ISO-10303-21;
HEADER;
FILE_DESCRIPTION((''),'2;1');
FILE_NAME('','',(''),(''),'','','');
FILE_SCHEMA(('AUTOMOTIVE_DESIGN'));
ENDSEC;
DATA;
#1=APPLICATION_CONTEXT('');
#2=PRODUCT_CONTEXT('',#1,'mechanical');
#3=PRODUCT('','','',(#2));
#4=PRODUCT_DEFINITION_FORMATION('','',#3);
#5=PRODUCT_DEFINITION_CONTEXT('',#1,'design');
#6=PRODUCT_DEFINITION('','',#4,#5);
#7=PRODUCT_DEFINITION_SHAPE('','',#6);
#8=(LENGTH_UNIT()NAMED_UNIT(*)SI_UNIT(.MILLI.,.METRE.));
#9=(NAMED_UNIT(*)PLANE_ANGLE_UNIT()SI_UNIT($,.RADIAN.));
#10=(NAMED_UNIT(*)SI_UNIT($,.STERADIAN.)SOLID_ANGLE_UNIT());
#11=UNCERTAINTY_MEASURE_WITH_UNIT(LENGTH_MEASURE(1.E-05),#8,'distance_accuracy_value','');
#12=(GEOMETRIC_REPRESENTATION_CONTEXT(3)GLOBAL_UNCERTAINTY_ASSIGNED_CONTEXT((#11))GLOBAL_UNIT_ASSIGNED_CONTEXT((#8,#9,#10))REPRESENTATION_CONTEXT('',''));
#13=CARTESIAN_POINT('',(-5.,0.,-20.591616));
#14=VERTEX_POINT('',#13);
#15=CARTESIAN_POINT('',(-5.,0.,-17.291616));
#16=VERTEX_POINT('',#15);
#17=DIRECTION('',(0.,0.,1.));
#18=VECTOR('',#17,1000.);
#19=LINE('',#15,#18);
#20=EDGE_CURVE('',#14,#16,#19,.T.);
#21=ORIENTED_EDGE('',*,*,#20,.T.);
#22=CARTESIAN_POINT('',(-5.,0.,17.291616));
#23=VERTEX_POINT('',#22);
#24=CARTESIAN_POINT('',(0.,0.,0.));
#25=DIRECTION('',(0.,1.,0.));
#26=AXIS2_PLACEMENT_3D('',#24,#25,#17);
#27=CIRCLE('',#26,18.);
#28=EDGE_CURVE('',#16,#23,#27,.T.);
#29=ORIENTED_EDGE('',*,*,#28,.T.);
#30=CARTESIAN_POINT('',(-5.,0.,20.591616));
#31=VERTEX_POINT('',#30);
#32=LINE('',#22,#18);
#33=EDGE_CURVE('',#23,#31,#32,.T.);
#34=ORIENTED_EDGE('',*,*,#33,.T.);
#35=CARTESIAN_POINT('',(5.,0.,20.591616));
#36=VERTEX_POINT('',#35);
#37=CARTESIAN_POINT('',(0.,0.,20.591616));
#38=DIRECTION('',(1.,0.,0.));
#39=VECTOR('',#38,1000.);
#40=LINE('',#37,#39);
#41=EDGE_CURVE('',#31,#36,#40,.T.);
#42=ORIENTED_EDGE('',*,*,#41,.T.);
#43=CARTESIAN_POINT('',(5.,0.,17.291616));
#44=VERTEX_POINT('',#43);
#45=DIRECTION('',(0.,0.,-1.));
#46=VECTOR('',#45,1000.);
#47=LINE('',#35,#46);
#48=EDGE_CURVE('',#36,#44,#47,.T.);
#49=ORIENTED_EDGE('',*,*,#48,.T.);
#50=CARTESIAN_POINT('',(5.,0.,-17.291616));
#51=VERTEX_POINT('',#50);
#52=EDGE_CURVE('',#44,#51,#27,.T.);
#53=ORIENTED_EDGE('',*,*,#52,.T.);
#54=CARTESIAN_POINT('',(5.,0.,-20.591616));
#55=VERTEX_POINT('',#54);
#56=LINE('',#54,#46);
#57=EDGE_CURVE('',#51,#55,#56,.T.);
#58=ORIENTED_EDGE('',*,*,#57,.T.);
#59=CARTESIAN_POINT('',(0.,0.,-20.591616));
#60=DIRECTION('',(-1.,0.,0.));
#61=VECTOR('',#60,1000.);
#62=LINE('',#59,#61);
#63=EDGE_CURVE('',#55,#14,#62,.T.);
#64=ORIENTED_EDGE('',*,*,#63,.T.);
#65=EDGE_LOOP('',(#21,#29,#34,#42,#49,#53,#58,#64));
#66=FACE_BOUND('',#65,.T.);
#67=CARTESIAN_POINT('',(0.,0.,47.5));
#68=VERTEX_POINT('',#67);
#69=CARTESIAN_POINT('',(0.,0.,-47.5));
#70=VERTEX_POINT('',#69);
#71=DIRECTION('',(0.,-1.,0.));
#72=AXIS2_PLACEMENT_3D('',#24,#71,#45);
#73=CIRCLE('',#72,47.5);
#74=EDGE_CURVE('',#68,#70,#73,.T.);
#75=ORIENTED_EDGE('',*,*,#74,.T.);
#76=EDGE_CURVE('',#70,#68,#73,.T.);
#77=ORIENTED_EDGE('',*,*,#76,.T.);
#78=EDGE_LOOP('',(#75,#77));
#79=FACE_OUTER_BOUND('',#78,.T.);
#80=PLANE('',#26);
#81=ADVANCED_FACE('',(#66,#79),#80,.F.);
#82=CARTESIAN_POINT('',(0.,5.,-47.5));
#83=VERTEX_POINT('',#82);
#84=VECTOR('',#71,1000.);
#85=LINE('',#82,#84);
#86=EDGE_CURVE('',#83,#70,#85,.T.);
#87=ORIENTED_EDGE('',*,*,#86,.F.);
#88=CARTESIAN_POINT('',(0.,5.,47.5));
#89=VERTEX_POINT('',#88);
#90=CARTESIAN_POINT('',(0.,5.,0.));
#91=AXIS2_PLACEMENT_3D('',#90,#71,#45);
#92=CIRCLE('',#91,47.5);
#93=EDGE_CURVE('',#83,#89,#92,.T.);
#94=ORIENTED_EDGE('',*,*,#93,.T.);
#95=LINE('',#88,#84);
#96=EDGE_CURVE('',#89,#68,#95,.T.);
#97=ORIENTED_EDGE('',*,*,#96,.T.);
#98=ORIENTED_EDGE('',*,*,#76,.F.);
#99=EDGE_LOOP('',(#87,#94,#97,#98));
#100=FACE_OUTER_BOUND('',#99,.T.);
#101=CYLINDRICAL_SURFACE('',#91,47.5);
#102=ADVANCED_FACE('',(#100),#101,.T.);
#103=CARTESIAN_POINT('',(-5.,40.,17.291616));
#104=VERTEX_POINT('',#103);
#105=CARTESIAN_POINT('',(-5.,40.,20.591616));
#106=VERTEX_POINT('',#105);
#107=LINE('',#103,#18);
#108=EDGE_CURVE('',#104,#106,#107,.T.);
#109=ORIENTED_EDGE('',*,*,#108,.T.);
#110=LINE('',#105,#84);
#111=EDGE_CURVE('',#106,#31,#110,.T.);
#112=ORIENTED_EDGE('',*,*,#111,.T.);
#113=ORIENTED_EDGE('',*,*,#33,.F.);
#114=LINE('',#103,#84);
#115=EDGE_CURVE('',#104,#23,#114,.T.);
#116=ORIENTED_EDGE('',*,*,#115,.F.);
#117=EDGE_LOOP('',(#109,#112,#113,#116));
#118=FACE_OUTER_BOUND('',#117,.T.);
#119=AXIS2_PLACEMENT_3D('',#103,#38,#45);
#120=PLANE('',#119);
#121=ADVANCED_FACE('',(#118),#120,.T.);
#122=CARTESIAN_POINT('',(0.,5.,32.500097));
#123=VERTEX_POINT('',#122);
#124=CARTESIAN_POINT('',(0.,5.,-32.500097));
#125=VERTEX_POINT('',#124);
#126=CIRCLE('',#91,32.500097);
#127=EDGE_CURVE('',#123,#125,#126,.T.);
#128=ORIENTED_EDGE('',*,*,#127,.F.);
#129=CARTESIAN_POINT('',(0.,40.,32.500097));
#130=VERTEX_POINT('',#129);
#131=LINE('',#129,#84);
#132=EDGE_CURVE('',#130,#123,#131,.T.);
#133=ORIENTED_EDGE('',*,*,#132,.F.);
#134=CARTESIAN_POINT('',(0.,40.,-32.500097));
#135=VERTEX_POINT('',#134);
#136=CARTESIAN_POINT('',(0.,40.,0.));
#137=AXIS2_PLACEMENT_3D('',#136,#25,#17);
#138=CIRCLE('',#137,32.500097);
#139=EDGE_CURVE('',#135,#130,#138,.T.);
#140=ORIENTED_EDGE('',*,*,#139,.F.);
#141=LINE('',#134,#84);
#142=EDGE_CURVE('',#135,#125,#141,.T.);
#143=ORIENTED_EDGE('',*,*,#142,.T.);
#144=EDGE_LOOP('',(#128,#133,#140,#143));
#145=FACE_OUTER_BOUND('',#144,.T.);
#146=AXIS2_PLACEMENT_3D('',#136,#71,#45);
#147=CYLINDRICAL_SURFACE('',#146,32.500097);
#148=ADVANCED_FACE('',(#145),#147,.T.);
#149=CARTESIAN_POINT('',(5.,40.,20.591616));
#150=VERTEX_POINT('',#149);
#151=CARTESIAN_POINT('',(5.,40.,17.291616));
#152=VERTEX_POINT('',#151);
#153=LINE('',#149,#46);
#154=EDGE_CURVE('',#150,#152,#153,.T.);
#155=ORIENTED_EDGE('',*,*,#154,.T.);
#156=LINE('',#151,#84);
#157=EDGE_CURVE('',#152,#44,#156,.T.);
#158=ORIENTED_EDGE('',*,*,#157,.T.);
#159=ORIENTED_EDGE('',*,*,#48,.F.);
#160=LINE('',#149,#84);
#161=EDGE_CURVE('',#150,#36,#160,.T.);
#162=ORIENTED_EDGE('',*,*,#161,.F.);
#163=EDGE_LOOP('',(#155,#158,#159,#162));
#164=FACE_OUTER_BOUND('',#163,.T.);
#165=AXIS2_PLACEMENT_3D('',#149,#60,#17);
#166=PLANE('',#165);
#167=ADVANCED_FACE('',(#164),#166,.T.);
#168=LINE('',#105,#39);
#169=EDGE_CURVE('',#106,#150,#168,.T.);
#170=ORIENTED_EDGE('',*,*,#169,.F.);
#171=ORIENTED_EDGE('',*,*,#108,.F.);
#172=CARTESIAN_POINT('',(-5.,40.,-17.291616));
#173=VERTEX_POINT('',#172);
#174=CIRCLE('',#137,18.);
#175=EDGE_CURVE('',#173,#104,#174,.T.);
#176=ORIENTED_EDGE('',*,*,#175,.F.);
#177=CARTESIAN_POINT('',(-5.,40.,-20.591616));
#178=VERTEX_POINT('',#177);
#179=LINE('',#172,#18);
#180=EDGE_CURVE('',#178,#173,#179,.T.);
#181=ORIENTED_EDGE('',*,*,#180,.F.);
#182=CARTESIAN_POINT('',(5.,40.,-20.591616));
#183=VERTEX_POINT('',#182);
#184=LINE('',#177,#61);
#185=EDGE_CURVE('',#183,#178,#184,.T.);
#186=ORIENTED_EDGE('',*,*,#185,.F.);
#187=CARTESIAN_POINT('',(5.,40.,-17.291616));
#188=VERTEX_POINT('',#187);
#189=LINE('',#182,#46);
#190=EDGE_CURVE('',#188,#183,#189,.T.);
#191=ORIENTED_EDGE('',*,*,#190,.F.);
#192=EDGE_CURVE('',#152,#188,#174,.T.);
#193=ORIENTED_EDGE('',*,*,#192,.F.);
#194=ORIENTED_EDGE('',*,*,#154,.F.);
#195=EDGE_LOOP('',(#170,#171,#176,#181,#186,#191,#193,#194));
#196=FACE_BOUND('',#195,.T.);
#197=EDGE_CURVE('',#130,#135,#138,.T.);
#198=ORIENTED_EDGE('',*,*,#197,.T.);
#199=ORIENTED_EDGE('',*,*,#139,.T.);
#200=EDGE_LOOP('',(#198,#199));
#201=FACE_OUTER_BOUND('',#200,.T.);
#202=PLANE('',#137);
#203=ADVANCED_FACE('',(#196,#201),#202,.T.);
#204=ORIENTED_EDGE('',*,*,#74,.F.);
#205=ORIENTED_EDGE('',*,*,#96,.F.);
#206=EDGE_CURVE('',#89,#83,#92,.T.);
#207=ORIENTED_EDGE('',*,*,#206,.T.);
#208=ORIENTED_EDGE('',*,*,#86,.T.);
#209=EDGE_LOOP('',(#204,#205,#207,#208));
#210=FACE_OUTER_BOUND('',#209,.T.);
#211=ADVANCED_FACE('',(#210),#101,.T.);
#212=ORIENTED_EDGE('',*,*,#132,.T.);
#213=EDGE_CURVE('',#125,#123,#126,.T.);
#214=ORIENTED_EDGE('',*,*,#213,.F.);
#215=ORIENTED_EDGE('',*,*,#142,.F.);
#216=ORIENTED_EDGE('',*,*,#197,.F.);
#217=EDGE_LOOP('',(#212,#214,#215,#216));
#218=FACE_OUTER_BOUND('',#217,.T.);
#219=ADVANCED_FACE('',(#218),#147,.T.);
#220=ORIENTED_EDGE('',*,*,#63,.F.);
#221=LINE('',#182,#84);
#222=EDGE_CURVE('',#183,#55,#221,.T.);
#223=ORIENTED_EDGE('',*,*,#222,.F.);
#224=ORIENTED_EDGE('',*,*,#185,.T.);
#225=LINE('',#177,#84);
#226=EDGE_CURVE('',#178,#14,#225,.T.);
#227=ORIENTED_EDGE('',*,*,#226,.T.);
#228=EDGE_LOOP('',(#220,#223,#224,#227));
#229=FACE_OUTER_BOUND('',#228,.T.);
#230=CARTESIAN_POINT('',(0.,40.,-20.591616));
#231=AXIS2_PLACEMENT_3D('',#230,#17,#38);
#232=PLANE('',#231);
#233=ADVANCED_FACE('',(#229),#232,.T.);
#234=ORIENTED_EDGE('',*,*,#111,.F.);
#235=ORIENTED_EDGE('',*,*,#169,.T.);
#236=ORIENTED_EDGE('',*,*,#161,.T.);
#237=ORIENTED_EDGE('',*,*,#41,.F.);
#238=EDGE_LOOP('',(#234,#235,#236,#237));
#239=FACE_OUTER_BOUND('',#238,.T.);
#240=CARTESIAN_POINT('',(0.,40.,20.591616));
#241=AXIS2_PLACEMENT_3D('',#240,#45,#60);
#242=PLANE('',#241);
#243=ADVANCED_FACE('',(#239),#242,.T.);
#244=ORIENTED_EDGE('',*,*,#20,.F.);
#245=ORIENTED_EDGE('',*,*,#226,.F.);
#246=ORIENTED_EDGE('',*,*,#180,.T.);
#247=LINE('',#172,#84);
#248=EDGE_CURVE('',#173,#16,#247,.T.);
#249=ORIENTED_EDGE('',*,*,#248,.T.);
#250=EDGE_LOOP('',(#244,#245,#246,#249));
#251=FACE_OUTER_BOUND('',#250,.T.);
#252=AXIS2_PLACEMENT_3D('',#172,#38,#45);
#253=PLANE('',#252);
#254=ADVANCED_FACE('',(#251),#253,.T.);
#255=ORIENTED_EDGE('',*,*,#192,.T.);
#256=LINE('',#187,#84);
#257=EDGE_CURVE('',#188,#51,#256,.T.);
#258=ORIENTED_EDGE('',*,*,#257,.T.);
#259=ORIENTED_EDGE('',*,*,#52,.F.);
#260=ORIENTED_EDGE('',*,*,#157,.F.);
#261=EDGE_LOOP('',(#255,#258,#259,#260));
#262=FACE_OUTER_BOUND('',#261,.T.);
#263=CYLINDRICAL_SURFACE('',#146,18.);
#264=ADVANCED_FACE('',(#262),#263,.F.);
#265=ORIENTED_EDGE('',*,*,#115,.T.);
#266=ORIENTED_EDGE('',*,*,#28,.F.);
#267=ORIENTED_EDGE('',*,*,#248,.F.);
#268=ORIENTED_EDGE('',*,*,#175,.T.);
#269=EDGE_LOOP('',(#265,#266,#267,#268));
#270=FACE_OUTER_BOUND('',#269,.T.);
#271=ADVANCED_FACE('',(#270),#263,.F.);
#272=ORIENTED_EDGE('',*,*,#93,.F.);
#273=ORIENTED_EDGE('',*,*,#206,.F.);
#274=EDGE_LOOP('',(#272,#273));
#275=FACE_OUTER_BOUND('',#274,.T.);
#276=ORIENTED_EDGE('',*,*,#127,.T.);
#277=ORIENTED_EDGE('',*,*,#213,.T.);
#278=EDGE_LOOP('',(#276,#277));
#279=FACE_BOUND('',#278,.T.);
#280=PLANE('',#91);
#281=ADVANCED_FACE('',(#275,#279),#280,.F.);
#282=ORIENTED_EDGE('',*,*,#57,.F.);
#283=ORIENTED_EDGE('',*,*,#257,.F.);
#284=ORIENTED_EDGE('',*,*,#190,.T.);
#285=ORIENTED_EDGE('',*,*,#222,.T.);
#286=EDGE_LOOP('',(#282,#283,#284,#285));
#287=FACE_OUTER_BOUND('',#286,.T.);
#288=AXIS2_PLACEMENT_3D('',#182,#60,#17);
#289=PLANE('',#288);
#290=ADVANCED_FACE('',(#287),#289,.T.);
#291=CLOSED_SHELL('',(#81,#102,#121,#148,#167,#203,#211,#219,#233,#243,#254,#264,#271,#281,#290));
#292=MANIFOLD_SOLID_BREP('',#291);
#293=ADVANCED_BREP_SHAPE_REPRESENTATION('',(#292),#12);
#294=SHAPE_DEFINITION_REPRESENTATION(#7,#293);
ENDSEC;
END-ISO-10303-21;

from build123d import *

# Parameters (mm, degrees)
SKETCH_1_R      = 32.500096928
EXTRUDE_1_DEPTH = 40
SKETCH_2_R      = 47.5
SKETCH_2_R_2    = 32.5
EXTRUDE_2_DEPTH = 5


with BuildPart() as part:
    # 草图1 → 凸台-拉伸1 (new body)
    with BuildSketch(Plane(origin=(0, 0, 0), x_dir=(1, 0, 0), z_dir=(0, 1, 0))):
        with Locations(Location((0, 0, 0), (0, 0, 270))):
            Circle(SKETCH_1_R)
        with BuildLine():
            Line((0, 20.591616466), (5, 20.591616466))
            Line((5, 20.591616466), (5, 17.291616466))
            ThreePointArc((5, 17.291616466), (18, 0), (5, -17.291616466))
            Line((5, -17.291616466), (5, -20.591616466))
            Line((5, -20.591616466), (0, -20.591616466))
            Line((0, -20.591616466), (-5, -20.591616466))
            Line((-5, -20.591616466), (-5, -17.291616466))
            ThreePointArc((-5, -17.291616466), (-18, 0), (-5, 17.291616466))
            Line((-5, 17.291616466), (-5, 20.591616466))
            Line((-5, 20.591616466), (0, 20.591616466))
        make_face(mode=Mode.SUBTRACT)
    extrude(amount=EXTRUDE_1_DEPTH)

    # 草图2 → 凸台-拉伸2 (add)
    with BuildSketch(Plane.XZ):
        with Locations(Location((0, 0, 0), (0, 0, 270))):
            Circle(SKETCH_2_R)
        Circle(SKETCH_2_R_2, mode=Mode.SUBTRACT)
    extrude(amount=-EXTRUDE_2_DEPTH)


solid = part.part
